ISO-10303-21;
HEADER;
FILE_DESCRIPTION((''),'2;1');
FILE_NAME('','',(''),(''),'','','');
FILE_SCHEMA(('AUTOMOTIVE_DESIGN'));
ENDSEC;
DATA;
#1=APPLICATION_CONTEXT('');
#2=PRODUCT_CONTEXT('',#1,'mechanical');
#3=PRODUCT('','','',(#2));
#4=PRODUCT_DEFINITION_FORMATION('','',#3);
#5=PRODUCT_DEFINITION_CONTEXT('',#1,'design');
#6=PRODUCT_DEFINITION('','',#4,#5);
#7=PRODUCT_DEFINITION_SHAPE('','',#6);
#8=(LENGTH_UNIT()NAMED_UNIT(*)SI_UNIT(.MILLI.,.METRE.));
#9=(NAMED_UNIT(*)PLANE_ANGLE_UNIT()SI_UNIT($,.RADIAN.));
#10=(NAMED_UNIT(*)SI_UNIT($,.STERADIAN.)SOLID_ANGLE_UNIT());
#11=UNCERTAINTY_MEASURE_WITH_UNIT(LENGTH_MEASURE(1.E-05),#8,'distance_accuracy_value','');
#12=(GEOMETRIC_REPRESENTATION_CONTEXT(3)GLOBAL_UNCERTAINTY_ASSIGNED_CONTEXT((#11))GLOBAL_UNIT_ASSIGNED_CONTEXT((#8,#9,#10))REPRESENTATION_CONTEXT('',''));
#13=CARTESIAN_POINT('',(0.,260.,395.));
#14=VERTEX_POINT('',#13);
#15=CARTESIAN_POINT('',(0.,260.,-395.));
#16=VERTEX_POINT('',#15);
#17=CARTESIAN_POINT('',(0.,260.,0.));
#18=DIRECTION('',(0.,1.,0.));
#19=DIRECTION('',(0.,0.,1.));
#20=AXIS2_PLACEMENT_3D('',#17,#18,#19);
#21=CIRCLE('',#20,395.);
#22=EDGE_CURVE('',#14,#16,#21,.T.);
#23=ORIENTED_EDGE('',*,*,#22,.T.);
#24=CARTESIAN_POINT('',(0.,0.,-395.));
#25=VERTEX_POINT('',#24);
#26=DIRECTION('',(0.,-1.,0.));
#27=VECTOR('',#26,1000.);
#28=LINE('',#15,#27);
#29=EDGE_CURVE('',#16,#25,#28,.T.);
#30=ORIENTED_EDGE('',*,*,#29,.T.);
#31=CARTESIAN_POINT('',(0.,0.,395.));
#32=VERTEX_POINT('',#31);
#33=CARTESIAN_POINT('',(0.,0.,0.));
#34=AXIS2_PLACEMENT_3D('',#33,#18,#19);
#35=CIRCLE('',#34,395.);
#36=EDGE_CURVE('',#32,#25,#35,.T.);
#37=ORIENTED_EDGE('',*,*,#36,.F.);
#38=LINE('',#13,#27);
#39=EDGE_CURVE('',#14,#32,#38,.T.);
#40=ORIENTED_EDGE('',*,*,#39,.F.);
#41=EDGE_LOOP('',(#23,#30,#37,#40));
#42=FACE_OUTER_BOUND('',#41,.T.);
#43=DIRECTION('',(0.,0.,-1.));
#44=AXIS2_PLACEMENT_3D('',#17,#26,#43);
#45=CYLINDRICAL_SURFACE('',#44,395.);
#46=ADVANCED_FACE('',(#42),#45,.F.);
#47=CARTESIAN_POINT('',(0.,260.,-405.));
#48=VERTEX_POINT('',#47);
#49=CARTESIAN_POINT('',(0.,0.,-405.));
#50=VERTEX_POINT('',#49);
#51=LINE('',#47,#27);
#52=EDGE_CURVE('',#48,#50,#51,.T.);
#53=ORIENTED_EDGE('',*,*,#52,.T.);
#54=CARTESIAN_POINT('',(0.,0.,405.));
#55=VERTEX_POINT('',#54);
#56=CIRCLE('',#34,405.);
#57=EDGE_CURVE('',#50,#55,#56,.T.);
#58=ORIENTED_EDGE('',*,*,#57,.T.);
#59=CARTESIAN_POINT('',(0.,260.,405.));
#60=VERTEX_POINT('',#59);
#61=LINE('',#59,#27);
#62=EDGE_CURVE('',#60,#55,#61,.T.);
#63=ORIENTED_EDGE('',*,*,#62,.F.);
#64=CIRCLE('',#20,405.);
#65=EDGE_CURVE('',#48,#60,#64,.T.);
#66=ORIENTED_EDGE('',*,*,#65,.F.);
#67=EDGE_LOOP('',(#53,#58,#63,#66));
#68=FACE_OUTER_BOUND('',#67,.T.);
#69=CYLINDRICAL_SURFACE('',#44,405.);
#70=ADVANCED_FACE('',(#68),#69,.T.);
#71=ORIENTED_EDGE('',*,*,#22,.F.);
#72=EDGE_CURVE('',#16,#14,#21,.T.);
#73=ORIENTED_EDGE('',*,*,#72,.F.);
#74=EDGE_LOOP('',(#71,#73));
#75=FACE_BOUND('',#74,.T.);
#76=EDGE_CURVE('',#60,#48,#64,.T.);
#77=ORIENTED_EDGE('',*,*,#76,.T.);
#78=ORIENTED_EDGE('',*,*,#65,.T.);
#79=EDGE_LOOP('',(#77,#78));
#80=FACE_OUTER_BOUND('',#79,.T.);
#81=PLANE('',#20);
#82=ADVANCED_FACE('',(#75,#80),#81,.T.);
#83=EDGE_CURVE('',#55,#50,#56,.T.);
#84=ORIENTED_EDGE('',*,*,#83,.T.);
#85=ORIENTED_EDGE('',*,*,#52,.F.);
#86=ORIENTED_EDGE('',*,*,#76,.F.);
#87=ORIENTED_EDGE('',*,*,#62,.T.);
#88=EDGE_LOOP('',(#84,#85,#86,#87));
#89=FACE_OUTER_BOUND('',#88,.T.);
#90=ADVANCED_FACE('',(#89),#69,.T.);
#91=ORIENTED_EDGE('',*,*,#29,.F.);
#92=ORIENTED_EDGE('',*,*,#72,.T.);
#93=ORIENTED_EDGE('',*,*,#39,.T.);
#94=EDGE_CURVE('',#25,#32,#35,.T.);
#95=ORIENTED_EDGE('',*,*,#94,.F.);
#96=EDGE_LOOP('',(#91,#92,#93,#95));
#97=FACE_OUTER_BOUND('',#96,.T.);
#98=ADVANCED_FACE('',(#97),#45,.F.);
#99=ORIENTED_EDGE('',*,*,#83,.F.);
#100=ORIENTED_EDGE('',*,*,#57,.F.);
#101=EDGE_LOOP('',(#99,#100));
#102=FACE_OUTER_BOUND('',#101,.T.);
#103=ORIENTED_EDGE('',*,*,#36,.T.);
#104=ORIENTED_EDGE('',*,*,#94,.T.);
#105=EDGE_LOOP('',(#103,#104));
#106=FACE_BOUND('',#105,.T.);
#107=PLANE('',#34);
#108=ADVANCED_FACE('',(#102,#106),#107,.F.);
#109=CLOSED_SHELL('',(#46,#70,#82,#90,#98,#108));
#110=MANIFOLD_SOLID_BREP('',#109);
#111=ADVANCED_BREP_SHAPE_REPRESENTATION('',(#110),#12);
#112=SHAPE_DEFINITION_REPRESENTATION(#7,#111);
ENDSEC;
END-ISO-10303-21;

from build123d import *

# Parameters (mm, degrees)
SKETCH1_R           = 405
SKETCH1_R_2         = 395
BOSS_EXTRUDE1_DEPTH = 260


with BuildPart() as part:
    # Sketch1 → Boss-Extrude1 (new body)
    with BuildSketch(Plane(origin=(0, 0, 0), x_dir=(1, 0, 0), z_dir=(0, 1, 0))):
        with Locations(Location((0, 0, 0), (0, 0, 270))):
            Circle(SKETCH1_R)
        with Locations(Location((0, 0, 0), (0, 0, 270))):
            Circle(SKETCH1_R_2, mode=Mode.SUBTRACT)
    extrude(amount=BOSS_EXTRUDE1_DEPTH)


solid = part.part
